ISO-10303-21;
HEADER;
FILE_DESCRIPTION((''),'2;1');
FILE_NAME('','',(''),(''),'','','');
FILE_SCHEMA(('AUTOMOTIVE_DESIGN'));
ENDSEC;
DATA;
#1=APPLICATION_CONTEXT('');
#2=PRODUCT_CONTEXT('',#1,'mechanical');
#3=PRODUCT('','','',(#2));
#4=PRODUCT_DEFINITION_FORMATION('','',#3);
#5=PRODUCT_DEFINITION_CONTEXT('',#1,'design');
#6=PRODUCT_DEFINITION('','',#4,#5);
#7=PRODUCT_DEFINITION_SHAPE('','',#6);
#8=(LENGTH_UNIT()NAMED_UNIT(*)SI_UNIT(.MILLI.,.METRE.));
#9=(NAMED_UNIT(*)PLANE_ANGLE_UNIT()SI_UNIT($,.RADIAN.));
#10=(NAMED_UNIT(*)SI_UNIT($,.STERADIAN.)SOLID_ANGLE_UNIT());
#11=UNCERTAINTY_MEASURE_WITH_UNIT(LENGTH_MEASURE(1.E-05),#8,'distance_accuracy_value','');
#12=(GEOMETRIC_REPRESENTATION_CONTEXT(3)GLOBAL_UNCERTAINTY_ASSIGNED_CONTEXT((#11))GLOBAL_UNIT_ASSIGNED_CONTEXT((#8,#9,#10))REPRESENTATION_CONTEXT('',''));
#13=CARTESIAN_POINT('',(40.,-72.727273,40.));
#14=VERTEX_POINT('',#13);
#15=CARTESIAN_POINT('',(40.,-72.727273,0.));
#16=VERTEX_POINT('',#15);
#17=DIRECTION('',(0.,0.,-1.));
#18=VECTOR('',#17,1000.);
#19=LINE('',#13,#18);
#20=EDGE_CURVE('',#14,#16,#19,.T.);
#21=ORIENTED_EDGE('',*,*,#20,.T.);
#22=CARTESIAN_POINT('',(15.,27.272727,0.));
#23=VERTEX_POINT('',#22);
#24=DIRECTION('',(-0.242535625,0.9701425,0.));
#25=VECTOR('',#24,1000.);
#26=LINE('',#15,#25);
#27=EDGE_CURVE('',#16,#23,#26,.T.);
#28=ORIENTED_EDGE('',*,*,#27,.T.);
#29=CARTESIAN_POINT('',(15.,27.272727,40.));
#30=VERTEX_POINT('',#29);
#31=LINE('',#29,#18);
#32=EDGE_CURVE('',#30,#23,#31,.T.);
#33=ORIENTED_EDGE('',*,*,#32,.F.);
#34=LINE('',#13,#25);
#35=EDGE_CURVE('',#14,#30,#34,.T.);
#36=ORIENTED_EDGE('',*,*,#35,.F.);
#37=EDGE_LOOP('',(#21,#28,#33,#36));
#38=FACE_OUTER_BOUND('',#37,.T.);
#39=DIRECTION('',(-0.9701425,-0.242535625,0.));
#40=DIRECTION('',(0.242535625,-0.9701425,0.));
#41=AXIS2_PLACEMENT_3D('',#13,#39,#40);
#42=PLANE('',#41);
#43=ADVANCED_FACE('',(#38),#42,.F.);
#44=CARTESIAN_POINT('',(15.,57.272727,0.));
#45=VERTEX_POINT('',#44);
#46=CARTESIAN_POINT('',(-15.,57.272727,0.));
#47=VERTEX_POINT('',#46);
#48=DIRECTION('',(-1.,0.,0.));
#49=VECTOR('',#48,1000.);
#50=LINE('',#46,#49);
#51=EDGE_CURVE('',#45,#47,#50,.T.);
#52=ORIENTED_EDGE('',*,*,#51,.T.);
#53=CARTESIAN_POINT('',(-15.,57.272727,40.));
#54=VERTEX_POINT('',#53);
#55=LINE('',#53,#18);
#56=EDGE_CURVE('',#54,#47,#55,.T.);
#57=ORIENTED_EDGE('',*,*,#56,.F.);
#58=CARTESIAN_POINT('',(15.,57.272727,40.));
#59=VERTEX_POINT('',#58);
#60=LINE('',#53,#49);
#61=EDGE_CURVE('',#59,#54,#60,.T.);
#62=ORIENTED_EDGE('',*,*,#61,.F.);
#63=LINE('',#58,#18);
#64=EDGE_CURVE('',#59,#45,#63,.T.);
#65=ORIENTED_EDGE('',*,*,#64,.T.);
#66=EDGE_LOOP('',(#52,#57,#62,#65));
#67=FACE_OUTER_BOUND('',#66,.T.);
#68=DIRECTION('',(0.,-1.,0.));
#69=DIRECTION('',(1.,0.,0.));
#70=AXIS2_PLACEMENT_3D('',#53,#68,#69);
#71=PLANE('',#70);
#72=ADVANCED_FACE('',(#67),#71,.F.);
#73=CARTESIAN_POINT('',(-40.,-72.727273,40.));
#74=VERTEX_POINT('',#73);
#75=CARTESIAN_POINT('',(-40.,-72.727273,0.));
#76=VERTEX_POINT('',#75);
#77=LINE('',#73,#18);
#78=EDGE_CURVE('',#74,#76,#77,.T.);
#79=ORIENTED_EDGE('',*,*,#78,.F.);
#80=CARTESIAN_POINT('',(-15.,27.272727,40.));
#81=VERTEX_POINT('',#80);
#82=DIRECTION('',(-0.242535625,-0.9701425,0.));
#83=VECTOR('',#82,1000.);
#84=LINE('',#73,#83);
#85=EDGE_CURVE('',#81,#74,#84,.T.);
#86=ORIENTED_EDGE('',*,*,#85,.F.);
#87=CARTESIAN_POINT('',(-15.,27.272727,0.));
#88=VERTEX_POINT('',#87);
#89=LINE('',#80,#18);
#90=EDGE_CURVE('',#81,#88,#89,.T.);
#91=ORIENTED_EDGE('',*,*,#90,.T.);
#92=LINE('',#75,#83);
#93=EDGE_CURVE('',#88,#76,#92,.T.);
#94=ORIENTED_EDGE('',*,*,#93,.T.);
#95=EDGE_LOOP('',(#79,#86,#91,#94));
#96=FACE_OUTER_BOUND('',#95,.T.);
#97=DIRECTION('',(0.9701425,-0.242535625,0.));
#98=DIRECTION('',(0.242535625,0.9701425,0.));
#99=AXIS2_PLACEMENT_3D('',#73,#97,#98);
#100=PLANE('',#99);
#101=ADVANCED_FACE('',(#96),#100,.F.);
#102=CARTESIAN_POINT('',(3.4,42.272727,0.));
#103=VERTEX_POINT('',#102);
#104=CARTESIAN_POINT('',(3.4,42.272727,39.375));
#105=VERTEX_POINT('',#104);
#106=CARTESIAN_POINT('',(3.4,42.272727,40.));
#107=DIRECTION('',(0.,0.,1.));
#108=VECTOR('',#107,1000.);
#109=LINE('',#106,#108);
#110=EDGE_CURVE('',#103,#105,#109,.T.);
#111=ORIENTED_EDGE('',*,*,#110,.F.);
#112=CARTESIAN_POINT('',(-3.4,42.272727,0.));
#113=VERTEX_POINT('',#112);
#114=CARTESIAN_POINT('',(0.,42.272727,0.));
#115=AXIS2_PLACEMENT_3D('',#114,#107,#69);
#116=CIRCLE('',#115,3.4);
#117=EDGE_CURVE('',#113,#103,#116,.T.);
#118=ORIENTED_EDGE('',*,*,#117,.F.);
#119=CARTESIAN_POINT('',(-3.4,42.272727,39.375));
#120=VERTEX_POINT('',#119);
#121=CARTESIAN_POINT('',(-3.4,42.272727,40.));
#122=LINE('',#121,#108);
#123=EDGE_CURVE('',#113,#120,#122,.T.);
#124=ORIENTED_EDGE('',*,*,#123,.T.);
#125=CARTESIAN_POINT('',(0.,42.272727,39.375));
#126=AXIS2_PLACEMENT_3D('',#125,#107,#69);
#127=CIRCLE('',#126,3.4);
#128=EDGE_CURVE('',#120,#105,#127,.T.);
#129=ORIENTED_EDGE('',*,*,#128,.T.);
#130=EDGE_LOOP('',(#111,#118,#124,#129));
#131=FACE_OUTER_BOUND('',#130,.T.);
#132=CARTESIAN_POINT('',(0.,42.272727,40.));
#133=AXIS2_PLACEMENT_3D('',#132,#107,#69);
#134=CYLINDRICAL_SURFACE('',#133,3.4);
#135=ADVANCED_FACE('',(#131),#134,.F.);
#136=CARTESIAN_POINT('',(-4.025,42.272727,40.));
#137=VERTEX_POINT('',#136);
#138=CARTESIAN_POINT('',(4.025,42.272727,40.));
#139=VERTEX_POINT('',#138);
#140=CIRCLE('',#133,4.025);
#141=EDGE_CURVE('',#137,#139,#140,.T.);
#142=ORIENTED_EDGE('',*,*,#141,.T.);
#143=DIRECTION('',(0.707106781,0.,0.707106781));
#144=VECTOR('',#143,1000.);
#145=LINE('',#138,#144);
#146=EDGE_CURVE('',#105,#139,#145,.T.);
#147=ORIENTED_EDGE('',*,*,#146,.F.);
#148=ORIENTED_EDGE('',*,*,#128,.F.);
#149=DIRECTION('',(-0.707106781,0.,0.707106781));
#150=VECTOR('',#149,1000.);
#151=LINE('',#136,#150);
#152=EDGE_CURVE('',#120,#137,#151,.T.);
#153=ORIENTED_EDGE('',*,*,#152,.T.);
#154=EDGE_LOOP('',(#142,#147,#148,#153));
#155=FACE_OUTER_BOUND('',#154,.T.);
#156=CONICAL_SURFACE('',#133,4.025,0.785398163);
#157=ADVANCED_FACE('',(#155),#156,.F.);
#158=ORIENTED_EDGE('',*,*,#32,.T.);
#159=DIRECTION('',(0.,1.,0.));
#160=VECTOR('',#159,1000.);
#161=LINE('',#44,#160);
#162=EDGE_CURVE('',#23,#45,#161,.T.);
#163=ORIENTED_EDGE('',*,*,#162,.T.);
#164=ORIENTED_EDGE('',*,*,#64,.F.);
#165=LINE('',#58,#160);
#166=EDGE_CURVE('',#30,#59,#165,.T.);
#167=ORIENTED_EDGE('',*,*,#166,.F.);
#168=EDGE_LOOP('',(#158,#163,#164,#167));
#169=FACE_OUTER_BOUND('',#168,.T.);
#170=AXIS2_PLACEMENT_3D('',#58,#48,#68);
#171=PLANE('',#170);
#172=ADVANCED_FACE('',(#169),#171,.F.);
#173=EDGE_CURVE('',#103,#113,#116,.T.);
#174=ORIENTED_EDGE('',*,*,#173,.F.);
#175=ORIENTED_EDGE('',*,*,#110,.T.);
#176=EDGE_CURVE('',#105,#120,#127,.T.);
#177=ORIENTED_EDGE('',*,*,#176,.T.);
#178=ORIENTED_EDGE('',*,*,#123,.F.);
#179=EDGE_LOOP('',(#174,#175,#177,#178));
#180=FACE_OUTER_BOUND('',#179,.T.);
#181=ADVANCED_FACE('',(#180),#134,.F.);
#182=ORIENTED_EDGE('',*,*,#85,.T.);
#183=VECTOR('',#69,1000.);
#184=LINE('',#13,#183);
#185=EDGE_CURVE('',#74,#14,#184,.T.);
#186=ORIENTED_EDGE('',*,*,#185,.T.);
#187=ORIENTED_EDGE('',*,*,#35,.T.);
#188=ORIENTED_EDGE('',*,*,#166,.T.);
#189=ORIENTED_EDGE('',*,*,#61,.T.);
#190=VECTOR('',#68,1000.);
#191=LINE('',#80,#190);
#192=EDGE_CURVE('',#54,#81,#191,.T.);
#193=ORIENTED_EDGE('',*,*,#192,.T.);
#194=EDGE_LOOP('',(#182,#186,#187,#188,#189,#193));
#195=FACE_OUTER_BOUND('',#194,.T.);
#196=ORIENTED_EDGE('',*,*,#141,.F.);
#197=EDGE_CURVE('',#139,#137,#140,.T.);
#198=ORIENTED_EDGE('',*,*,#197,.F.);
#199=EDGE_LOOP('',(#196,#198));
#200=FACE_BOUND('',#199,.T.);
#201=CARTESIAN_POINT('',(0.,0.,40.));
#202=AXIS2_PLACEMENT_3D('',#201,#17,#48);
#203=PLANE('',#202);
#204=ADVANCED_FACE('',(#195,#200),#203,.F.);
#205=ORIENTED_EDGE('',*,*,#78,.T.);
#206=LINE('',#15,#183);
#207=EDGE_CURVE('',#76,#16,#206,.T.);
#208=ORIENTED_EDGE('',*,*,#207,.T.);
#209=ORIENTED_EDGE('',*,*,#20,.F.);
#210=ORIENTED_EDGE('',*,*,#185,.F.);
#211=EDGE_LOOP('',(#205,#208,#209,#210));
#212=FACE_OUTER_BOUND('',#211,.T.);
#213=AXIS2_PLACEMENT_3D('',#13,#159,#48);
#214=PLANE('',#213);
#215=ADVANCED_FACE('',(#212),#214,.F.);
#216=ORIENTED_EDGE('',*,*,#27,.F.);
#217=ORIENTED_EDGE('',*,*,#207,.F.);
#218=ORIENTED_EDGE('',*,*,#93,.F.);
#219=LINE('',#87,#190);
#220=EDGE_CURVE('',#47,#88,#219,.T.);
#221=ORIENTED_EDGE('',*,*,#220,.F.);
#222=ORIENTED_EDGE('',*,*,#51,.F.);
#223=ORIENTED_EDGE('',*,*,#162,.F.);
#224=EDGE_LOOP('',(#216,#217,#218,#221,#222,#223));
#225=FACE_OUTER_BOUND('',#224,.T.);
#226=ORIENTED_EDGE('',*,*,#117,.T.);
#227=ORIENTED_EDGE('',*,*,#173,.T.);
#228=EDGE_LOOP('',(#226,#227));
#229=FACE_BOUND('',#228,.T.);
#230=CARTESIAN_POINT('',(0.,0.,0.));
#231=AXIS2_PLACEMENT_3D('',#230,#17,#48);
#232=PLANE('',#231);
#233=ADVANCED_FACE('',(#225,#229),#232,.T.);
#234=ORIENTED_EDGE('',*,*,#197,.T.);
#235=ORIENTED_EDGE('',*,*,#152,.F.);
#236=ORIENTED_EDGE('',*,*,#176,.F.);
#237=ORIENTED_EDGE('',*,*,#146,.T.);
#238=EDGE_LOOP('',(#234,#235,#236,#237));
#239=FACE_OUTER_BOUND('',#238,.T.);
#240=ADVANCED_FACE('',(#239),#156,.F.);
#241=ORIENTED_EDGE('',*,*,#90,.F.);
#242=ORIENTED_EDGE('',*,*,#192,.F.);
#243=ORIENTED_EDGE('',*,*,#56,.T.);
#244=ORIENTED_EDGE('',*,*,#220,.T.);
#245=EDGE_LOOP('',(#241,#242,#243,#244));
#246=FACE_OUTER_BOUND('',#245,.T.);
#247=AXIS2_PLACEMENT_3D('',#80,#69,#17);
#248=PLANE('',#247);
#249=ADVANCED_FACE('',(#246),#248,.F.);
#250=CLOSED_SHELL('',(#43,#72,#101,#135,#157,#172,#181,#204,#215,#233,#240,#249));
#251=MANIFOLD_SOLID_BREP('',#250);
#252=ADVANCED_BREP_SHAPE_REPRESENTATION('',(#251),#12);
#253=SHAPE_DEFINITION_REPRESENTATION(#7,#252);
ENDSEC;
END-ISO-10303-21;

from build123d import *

# Parameters (mm, degrees)
BOSS_EXTRUDE1_DEPTH         = 40
M8_TAPPED_HOLE1_D           = 6.8
M8_TAPPED_HOLE1_CSINK_D     = 8.05
M8_TAPPED_HOLE1_CSINK_ANGLE = 90


with BuildPart() as part:
    # Sketch1 → Boss-Extrude1 (new body)
    with BuildSketch(Plane.XY):
        Polygon((40, -72.727272727), (-40, -72.727272727), (-15, 27.272727273), (-15, 57.272727273), (15, 57.272727273), (15, 27.272727273), align=None)
    extrude(amount=BOSS_EXTRUDE1_DEPTH)

    # M8 Tapped Hole1 (through all)
    with Locations(Plane.XY.offset(40)):
        with Locations((0, 42.272727273)):
            CounterSinkHole(M8_TAPPED_HOLE1_D / 2, M8_TAPPED_HOLE1_CSINK_D / 2, counter_sink_angle=M8_TAPPED_HOLE1_CSINK_ANGLE)


solid = part.part
